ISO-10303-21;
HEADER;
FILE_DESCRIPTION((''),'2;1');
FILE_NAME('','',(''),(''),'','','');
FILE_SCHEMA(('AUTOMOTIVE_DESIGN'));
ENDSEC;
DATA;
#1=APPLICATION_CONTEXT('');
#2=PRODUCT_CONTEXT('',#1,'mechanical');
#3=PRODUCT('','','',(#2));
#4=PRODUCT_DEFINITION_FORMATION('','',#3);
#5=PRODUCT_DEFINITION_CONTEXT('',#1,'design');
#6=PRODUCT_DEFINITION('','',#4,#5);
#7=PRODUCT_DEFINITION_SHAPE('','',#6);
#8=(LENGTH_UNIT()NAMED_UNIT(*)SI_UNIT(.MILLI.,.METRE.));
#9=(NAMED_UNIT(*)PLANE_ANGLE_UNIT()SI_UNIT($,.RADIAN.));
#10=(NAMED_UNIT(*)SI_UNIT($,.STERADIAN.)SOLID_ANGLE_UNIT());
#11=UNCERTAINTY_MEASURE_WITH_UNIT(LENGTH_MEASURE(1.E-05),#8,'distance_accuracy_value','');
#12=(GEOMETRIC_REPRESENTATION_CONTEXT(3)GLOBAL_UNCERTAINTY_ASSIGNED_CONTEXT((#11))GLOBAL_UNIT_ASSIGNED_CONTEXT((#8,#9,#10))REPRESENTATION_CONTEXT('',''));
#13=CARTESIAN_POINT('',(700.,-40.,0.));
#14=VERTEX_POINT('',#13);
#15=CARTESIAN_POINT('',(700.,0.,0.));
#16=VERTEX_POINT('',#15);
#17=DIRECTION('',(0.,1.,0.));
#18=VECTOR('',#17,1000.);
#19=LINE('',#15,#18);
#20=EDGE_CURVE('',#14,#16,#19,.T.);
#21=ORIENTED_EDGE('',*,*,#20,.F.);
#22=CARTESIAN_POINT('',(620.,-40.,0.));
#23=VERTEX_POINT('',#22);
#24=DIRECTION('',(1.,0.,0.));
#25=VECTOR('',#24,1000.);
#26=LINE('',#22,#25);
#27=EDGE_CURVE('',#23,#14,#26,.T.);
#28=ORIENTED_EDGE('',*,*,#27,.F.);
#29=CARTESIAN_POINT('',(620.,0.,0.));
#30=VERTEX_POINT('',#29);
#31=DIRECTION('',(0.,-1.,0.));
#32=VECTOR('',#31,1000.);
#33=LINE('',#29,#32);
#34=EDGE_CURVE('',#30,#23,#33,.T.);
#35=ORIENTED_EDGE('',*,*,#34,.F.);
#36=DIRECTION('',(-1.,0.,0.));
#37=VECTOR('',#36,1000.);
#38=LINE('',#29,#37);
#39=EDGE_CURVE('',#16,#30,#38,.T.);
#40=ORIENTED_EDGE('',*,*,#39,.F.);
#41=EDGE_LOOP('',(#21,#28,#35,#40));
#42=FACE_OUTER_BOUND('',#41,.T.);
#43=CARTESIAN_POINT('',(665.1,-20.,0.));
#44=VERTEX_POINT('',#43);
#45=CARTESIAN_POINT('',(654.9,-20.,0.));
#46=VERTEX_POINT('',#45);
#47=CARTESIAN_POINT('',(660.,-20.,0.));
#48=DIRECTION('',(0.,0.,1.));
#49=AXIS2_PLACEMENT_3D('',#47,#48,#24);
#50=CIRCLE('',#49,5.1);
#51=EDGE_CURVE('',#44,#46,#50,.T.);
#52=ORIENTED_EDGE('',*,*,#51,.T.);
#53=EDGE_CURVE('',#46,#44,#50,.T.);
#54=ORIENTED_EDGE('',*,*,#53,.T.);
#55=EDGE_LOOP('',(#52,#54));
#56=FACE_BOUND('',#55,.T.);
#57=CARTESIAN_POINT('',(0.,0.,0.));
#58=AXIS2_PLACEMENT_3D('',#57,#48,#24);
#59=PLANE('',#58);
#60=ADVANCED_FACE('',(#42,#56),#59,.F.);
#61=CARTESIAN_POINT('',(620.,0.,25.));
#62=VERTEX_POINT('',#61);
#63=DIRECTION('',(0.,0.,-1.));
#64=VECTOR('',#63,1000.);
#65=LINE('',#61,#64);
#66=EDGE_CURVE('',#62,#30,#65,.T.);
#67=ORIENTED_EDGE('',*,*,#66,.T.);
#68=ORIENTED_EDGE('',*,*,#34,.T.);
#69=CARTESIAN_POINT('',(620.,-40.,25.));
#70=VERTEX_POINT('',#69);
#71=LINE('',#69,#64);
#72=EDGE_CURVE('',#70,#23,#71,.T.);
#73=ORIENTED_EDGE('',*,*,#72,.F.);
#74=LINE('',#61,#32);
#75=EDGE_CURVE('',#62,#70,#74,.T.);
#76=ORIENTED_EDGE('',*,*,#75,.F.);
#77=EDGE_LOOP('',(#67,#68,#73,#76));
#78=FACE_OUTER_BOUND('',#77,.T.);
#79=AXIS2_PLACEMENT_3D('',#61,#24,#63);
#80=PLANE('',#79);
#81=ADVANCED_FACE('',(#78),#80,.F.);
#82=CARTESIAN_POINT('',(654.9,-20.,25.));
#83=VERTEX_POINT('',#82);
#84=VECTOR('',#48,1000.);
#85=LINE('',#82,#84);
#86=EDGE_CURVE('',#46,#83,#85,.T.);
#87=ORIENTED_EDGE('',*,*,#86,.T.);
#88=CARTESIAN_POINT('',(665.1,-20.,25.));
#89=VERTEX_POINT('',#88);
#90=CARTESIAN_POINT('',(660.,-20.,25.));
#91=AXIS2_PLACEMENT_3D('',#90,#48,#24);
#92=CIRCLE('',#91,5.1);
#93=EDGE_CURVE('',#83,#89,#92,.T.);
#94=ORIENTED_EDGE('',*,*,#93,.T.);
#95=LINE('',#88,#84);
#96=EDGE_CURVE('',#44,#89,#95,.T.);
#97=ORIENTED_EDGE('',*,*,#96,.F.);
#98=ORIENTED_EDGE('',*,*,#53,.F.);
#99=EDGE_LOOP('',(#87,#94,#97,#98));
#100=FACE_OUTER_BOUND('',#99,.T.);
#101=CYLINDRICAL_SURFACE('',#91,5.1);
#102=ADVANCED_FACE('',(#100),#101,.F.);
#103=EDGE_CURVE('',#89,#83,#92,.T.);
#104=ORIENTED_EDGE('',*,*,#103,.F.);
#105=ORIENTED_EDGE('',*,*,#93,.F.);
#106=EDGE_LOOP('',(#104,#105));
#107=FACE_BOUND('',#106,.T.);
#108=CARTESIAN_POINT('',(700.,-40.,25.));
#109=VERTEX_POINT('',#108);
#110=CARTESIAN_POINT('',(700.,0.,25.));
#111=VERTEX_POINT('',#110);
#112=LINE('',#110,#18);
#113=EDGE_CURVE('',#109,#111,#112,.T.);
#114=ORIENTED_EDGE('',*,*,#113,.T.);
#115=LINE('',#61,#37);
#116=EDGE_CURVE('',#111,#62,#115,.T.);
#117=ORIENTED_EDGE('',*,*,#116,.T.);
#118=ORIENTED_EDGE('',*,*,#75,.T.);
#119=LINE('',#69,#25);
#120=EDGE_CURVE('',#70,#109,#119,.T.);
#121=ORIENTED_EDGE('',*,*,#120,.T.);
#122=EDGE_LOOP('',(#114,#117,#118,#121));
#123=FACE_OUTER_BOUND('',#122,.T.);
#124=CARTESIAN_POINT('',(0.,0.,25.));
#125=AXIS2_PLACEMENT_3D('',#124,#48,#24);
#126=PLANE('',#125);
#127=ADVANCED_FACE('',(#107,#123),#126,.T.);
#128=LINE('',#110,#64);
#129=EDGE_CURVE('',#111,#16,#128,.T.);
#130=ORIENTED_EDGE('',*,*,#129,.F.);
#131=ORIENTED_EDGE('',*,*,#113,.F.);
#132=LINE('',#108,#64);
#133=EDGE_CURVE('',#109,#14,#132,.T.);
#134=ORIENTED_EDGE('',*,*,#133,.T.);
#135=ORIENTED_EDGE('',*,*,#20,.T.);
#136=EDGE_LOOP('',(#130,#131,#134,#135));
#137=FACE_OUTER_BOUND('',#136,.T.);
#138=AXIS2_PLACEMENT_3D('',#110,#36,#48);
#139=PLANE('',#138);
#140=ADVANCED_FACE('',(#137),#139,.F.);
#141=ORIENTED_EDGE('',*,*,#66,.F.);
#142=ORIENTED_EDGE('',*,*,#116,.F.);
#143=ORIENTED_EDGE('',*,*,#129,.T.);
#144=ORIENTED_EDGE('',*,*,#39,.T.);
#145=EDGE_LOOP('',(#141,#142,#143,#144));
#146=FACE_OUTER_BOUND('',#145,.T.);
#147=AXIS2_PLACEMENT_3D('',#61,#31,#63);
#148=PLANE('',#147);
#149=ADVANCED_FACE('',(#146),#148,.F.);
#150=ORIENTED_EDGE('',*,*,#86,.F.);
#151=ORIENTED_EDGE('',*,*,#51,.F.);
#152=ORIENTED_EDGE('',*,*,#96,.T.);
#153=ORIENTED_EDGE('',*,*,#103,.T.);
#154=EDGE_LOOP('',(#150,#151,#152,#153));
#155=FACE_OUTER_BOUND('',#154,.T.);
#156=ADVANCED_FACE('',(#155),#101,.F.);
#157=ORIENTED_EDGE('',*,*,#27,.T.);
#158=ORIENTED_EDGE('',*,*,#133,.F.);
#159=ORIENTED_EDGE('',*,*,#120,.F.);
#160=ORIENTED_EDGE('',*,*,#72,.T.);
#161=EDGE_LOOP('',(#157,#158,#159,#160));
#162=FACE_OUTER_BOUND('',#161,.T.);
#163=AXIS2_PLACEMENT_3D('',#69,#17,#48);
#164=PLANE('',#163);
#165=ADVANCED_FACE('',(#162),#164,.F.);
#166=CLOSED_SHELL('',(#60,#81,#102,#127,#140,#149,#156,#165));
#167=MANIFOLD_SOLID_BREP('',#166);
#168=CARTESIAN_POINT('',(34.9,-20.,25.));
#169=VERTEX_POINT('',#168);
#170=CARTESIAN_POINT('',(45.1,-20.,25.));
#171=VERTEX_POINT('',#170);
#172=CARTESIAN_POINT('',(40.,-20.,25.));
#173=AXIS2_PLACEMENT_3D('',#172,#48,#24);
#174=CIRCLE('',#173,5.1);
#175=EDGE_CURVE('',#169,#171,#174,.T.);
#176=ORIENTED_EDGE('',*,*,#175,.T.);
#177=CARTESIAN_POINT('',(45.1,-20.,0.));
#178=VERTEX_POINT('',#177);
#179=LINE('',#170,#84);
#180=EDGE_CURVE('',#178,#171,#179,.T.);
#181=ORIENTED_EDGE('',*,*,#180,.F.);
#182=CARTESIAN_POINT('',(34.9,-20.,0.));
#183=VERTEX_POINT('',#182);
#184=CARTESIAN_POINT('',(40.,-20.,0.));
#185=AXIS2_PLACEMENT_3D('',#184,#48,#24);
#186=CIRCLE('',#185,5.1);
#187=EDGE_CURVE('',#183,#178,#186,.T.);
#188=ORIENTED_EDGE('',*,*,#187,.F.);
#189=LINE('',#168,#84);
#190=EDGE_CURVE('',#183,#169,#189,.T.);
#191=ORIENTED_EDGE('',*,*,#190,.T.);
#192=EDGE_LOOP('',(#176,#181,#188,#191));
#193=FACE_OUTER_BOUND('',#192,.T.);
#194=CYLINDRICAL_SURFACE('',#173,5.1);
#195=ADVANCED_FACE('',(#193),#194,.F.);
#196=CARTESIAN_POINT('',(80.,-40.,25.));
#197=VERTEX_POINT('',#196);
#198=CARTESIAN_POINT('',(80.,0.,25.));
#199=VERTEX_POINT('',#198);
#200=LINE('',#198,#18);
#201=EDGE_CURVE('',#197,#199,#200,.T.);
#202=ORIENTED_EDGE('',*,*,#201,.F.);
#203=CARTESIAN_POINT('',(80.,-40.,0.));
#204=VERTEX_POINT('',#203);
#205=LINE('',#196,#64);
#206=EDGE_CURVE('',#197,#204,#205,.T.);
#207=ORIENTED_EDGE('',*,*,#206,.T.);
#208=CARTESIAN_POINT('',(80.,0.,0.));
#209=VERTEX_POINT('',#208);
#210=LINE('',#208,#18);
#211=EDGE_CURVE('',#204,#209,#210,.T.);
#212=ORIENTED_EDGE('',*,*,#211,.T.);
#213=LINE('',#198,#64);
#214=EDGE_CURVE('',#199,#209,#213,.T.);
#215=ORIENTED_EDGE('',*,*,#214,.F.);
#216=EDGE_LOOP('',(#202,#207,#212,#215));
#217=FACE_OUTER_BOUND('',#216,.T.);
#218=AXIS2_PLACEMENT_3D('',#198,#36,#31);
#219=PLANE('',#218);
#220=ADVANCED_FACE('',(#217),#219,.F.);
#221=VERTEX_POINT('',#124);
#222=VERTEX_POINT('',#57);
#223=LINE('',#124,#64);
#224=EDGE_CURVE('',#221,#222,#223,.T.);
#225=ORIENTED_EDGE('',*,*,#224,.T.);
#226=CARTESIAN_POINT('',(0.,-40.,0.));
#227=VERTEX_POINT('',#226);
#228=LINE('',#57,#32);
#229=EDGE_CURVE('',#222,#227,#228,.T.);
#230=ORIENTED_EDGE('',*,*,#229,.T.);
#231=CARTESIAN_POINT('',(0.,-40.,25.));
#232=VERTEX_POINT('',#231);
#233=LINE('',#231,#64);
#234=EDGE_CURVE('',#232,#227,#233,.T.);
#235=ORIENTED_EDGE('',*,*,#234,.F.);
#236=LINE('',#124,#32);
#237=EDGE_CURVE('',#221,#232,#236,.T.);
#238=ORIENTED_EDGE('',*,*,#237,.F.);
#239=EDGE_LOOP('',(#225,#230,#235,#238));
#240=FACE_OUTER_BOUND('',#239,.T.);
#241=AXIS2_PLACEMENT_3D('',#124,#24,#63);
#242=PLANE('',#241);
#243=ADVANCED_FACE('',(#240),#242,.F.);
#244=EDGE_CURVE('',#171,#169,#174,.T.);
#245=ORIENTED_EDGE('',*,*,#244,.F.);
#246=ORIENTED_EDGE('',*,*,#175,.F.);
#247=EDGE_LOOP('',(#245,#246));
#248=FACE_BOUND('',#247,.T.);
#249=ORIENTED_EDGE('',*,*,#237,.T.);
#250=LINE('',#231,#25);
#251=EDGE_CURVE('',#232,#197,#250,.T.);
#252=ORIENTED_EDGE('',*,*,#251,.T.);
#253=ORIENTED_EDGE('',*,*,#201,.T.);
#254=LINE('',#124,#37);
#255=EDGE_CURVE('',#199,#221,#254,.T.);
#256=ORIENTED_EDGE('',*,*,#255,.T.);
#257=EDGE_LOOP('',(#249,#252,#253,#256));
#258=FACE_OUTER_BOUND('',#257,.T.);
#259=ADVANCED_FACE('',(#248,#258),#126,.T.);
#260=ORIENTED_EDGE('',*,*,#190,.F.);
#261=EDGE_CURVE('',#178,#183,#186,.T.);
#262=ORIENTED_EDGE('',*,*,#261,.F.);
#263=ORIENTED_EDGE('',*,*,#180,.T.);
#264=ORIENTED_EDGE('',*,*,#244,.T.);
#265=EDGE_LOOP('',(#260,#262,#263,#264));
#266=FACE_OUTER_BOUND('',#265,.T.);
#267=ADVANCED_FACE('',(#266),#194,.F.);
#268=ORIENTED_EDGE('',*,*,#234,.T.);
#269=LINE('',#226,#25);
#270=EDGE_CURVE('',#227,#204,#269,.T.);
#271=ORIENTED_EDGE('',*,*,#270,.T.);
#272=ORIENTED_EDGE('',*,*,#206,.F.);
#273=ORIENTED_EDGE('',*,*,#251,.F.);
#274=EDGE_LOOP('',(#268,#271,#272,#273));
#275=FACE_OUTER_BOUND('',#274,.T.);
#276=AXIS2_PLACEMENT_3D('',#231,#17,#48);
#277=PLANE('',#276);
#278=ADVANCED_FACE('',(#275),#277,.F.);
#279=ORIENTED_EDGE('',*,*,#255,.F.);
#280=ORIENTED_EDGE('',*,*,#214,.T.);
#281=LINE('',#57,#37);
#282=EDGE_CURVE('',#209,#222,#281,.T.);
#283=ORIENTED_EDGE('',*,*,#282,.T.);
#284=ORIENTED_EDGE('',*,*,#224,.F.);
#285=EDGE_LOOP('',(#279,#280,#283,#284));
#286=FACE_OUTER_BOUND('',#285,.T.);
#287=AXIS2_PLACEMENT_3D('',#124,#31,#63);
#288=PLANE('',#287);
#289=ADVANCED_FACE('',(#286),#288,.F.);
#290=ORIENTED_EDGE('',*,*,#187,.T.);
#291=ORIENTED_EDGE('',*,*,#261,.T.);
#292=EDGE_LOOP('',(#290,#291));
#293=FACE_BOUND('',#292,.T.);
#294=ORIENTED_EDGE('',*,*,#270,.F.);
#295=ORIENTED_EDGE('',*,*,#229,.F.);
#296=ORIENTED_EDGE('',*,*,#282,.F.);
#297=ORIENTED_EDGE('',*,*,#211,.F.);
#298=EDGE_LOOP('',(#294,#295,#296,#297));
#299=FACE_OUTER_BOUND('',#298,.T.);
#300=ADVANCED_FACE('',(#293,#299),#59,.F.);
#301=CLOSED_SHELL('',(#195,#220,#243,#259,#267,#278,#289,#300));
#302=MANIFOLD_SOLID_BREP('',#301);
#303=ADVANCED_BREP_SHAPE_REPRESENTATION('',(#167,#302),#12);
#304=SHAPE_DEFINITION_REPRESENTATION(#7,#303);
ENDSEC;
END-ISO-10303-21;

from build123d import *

# Parameters (mm, degrees)
SKETCH1_W                   = 80
SKETCH1_H                   = 40
BOSS_EXTRUDE1_DEPTH         = 25
BOSS_EXTRUDE1_2_DEPTH       = 25
SKETCH3_W                   = 5.1
SKETCH3_H                   = 25
M12_TAPPED_HOLE1_AT_2_COUNT = 2
M12_TAPPED_HOLE1_AT_2_PITCH = 620


with BuildPart() as part:
    # Sketch1 → Boss-Extrude1 (new body)
    with BuildSketch(Plane.XY):
        with Locations((40, -20)):
            Rectangle(SKETCH1_W, SKETCH1_H)
    extrude(amount=BOSS_EXTRUDE1_DEPTH)

    # Sketch3 → M12 Tapped Hole1 (revolve, cut)
    with BuildSketch(Plane(origin=(40, -20, 25), x_dir=(0, -1, 0), z_dir=(1, 0, 0))):
        with Locations((2.55, 12.5)):
            Rectangle(SKETCH3_W, SKETCH3_H)
    m12_tapped_hole1 = revolve(axis=Axis((40, -20, 31.35), (0, 0, -1)), mode=Mode.SUBTRACT)


with BuildPart() as body_2:
    # Sketch1 → Boss-Extrude1 2 (new body)
    with BuildSketch(Plane.XY):
        with Locations((660, -20)):
            Rectangle(SKETCH1_W, SKETCH1_H)
    extrude(amount=BOSS_EXTRUDE1_2_DEPTH)

    # M12 Tapped Hole1 at 2: M12 Tapped Hole1 ×2
    with Locations(*[(i * M12_TAPPED_HOLE1_AT_2_PITCH, 0, 0) for i in range(1, M12_TAPPED_HOLE1_AT_2_COUNT)]):
        add(m12_tapped_hole1, mode=Mode.SUBTRACT)


solid = Compound([part.part, body_2.part])
